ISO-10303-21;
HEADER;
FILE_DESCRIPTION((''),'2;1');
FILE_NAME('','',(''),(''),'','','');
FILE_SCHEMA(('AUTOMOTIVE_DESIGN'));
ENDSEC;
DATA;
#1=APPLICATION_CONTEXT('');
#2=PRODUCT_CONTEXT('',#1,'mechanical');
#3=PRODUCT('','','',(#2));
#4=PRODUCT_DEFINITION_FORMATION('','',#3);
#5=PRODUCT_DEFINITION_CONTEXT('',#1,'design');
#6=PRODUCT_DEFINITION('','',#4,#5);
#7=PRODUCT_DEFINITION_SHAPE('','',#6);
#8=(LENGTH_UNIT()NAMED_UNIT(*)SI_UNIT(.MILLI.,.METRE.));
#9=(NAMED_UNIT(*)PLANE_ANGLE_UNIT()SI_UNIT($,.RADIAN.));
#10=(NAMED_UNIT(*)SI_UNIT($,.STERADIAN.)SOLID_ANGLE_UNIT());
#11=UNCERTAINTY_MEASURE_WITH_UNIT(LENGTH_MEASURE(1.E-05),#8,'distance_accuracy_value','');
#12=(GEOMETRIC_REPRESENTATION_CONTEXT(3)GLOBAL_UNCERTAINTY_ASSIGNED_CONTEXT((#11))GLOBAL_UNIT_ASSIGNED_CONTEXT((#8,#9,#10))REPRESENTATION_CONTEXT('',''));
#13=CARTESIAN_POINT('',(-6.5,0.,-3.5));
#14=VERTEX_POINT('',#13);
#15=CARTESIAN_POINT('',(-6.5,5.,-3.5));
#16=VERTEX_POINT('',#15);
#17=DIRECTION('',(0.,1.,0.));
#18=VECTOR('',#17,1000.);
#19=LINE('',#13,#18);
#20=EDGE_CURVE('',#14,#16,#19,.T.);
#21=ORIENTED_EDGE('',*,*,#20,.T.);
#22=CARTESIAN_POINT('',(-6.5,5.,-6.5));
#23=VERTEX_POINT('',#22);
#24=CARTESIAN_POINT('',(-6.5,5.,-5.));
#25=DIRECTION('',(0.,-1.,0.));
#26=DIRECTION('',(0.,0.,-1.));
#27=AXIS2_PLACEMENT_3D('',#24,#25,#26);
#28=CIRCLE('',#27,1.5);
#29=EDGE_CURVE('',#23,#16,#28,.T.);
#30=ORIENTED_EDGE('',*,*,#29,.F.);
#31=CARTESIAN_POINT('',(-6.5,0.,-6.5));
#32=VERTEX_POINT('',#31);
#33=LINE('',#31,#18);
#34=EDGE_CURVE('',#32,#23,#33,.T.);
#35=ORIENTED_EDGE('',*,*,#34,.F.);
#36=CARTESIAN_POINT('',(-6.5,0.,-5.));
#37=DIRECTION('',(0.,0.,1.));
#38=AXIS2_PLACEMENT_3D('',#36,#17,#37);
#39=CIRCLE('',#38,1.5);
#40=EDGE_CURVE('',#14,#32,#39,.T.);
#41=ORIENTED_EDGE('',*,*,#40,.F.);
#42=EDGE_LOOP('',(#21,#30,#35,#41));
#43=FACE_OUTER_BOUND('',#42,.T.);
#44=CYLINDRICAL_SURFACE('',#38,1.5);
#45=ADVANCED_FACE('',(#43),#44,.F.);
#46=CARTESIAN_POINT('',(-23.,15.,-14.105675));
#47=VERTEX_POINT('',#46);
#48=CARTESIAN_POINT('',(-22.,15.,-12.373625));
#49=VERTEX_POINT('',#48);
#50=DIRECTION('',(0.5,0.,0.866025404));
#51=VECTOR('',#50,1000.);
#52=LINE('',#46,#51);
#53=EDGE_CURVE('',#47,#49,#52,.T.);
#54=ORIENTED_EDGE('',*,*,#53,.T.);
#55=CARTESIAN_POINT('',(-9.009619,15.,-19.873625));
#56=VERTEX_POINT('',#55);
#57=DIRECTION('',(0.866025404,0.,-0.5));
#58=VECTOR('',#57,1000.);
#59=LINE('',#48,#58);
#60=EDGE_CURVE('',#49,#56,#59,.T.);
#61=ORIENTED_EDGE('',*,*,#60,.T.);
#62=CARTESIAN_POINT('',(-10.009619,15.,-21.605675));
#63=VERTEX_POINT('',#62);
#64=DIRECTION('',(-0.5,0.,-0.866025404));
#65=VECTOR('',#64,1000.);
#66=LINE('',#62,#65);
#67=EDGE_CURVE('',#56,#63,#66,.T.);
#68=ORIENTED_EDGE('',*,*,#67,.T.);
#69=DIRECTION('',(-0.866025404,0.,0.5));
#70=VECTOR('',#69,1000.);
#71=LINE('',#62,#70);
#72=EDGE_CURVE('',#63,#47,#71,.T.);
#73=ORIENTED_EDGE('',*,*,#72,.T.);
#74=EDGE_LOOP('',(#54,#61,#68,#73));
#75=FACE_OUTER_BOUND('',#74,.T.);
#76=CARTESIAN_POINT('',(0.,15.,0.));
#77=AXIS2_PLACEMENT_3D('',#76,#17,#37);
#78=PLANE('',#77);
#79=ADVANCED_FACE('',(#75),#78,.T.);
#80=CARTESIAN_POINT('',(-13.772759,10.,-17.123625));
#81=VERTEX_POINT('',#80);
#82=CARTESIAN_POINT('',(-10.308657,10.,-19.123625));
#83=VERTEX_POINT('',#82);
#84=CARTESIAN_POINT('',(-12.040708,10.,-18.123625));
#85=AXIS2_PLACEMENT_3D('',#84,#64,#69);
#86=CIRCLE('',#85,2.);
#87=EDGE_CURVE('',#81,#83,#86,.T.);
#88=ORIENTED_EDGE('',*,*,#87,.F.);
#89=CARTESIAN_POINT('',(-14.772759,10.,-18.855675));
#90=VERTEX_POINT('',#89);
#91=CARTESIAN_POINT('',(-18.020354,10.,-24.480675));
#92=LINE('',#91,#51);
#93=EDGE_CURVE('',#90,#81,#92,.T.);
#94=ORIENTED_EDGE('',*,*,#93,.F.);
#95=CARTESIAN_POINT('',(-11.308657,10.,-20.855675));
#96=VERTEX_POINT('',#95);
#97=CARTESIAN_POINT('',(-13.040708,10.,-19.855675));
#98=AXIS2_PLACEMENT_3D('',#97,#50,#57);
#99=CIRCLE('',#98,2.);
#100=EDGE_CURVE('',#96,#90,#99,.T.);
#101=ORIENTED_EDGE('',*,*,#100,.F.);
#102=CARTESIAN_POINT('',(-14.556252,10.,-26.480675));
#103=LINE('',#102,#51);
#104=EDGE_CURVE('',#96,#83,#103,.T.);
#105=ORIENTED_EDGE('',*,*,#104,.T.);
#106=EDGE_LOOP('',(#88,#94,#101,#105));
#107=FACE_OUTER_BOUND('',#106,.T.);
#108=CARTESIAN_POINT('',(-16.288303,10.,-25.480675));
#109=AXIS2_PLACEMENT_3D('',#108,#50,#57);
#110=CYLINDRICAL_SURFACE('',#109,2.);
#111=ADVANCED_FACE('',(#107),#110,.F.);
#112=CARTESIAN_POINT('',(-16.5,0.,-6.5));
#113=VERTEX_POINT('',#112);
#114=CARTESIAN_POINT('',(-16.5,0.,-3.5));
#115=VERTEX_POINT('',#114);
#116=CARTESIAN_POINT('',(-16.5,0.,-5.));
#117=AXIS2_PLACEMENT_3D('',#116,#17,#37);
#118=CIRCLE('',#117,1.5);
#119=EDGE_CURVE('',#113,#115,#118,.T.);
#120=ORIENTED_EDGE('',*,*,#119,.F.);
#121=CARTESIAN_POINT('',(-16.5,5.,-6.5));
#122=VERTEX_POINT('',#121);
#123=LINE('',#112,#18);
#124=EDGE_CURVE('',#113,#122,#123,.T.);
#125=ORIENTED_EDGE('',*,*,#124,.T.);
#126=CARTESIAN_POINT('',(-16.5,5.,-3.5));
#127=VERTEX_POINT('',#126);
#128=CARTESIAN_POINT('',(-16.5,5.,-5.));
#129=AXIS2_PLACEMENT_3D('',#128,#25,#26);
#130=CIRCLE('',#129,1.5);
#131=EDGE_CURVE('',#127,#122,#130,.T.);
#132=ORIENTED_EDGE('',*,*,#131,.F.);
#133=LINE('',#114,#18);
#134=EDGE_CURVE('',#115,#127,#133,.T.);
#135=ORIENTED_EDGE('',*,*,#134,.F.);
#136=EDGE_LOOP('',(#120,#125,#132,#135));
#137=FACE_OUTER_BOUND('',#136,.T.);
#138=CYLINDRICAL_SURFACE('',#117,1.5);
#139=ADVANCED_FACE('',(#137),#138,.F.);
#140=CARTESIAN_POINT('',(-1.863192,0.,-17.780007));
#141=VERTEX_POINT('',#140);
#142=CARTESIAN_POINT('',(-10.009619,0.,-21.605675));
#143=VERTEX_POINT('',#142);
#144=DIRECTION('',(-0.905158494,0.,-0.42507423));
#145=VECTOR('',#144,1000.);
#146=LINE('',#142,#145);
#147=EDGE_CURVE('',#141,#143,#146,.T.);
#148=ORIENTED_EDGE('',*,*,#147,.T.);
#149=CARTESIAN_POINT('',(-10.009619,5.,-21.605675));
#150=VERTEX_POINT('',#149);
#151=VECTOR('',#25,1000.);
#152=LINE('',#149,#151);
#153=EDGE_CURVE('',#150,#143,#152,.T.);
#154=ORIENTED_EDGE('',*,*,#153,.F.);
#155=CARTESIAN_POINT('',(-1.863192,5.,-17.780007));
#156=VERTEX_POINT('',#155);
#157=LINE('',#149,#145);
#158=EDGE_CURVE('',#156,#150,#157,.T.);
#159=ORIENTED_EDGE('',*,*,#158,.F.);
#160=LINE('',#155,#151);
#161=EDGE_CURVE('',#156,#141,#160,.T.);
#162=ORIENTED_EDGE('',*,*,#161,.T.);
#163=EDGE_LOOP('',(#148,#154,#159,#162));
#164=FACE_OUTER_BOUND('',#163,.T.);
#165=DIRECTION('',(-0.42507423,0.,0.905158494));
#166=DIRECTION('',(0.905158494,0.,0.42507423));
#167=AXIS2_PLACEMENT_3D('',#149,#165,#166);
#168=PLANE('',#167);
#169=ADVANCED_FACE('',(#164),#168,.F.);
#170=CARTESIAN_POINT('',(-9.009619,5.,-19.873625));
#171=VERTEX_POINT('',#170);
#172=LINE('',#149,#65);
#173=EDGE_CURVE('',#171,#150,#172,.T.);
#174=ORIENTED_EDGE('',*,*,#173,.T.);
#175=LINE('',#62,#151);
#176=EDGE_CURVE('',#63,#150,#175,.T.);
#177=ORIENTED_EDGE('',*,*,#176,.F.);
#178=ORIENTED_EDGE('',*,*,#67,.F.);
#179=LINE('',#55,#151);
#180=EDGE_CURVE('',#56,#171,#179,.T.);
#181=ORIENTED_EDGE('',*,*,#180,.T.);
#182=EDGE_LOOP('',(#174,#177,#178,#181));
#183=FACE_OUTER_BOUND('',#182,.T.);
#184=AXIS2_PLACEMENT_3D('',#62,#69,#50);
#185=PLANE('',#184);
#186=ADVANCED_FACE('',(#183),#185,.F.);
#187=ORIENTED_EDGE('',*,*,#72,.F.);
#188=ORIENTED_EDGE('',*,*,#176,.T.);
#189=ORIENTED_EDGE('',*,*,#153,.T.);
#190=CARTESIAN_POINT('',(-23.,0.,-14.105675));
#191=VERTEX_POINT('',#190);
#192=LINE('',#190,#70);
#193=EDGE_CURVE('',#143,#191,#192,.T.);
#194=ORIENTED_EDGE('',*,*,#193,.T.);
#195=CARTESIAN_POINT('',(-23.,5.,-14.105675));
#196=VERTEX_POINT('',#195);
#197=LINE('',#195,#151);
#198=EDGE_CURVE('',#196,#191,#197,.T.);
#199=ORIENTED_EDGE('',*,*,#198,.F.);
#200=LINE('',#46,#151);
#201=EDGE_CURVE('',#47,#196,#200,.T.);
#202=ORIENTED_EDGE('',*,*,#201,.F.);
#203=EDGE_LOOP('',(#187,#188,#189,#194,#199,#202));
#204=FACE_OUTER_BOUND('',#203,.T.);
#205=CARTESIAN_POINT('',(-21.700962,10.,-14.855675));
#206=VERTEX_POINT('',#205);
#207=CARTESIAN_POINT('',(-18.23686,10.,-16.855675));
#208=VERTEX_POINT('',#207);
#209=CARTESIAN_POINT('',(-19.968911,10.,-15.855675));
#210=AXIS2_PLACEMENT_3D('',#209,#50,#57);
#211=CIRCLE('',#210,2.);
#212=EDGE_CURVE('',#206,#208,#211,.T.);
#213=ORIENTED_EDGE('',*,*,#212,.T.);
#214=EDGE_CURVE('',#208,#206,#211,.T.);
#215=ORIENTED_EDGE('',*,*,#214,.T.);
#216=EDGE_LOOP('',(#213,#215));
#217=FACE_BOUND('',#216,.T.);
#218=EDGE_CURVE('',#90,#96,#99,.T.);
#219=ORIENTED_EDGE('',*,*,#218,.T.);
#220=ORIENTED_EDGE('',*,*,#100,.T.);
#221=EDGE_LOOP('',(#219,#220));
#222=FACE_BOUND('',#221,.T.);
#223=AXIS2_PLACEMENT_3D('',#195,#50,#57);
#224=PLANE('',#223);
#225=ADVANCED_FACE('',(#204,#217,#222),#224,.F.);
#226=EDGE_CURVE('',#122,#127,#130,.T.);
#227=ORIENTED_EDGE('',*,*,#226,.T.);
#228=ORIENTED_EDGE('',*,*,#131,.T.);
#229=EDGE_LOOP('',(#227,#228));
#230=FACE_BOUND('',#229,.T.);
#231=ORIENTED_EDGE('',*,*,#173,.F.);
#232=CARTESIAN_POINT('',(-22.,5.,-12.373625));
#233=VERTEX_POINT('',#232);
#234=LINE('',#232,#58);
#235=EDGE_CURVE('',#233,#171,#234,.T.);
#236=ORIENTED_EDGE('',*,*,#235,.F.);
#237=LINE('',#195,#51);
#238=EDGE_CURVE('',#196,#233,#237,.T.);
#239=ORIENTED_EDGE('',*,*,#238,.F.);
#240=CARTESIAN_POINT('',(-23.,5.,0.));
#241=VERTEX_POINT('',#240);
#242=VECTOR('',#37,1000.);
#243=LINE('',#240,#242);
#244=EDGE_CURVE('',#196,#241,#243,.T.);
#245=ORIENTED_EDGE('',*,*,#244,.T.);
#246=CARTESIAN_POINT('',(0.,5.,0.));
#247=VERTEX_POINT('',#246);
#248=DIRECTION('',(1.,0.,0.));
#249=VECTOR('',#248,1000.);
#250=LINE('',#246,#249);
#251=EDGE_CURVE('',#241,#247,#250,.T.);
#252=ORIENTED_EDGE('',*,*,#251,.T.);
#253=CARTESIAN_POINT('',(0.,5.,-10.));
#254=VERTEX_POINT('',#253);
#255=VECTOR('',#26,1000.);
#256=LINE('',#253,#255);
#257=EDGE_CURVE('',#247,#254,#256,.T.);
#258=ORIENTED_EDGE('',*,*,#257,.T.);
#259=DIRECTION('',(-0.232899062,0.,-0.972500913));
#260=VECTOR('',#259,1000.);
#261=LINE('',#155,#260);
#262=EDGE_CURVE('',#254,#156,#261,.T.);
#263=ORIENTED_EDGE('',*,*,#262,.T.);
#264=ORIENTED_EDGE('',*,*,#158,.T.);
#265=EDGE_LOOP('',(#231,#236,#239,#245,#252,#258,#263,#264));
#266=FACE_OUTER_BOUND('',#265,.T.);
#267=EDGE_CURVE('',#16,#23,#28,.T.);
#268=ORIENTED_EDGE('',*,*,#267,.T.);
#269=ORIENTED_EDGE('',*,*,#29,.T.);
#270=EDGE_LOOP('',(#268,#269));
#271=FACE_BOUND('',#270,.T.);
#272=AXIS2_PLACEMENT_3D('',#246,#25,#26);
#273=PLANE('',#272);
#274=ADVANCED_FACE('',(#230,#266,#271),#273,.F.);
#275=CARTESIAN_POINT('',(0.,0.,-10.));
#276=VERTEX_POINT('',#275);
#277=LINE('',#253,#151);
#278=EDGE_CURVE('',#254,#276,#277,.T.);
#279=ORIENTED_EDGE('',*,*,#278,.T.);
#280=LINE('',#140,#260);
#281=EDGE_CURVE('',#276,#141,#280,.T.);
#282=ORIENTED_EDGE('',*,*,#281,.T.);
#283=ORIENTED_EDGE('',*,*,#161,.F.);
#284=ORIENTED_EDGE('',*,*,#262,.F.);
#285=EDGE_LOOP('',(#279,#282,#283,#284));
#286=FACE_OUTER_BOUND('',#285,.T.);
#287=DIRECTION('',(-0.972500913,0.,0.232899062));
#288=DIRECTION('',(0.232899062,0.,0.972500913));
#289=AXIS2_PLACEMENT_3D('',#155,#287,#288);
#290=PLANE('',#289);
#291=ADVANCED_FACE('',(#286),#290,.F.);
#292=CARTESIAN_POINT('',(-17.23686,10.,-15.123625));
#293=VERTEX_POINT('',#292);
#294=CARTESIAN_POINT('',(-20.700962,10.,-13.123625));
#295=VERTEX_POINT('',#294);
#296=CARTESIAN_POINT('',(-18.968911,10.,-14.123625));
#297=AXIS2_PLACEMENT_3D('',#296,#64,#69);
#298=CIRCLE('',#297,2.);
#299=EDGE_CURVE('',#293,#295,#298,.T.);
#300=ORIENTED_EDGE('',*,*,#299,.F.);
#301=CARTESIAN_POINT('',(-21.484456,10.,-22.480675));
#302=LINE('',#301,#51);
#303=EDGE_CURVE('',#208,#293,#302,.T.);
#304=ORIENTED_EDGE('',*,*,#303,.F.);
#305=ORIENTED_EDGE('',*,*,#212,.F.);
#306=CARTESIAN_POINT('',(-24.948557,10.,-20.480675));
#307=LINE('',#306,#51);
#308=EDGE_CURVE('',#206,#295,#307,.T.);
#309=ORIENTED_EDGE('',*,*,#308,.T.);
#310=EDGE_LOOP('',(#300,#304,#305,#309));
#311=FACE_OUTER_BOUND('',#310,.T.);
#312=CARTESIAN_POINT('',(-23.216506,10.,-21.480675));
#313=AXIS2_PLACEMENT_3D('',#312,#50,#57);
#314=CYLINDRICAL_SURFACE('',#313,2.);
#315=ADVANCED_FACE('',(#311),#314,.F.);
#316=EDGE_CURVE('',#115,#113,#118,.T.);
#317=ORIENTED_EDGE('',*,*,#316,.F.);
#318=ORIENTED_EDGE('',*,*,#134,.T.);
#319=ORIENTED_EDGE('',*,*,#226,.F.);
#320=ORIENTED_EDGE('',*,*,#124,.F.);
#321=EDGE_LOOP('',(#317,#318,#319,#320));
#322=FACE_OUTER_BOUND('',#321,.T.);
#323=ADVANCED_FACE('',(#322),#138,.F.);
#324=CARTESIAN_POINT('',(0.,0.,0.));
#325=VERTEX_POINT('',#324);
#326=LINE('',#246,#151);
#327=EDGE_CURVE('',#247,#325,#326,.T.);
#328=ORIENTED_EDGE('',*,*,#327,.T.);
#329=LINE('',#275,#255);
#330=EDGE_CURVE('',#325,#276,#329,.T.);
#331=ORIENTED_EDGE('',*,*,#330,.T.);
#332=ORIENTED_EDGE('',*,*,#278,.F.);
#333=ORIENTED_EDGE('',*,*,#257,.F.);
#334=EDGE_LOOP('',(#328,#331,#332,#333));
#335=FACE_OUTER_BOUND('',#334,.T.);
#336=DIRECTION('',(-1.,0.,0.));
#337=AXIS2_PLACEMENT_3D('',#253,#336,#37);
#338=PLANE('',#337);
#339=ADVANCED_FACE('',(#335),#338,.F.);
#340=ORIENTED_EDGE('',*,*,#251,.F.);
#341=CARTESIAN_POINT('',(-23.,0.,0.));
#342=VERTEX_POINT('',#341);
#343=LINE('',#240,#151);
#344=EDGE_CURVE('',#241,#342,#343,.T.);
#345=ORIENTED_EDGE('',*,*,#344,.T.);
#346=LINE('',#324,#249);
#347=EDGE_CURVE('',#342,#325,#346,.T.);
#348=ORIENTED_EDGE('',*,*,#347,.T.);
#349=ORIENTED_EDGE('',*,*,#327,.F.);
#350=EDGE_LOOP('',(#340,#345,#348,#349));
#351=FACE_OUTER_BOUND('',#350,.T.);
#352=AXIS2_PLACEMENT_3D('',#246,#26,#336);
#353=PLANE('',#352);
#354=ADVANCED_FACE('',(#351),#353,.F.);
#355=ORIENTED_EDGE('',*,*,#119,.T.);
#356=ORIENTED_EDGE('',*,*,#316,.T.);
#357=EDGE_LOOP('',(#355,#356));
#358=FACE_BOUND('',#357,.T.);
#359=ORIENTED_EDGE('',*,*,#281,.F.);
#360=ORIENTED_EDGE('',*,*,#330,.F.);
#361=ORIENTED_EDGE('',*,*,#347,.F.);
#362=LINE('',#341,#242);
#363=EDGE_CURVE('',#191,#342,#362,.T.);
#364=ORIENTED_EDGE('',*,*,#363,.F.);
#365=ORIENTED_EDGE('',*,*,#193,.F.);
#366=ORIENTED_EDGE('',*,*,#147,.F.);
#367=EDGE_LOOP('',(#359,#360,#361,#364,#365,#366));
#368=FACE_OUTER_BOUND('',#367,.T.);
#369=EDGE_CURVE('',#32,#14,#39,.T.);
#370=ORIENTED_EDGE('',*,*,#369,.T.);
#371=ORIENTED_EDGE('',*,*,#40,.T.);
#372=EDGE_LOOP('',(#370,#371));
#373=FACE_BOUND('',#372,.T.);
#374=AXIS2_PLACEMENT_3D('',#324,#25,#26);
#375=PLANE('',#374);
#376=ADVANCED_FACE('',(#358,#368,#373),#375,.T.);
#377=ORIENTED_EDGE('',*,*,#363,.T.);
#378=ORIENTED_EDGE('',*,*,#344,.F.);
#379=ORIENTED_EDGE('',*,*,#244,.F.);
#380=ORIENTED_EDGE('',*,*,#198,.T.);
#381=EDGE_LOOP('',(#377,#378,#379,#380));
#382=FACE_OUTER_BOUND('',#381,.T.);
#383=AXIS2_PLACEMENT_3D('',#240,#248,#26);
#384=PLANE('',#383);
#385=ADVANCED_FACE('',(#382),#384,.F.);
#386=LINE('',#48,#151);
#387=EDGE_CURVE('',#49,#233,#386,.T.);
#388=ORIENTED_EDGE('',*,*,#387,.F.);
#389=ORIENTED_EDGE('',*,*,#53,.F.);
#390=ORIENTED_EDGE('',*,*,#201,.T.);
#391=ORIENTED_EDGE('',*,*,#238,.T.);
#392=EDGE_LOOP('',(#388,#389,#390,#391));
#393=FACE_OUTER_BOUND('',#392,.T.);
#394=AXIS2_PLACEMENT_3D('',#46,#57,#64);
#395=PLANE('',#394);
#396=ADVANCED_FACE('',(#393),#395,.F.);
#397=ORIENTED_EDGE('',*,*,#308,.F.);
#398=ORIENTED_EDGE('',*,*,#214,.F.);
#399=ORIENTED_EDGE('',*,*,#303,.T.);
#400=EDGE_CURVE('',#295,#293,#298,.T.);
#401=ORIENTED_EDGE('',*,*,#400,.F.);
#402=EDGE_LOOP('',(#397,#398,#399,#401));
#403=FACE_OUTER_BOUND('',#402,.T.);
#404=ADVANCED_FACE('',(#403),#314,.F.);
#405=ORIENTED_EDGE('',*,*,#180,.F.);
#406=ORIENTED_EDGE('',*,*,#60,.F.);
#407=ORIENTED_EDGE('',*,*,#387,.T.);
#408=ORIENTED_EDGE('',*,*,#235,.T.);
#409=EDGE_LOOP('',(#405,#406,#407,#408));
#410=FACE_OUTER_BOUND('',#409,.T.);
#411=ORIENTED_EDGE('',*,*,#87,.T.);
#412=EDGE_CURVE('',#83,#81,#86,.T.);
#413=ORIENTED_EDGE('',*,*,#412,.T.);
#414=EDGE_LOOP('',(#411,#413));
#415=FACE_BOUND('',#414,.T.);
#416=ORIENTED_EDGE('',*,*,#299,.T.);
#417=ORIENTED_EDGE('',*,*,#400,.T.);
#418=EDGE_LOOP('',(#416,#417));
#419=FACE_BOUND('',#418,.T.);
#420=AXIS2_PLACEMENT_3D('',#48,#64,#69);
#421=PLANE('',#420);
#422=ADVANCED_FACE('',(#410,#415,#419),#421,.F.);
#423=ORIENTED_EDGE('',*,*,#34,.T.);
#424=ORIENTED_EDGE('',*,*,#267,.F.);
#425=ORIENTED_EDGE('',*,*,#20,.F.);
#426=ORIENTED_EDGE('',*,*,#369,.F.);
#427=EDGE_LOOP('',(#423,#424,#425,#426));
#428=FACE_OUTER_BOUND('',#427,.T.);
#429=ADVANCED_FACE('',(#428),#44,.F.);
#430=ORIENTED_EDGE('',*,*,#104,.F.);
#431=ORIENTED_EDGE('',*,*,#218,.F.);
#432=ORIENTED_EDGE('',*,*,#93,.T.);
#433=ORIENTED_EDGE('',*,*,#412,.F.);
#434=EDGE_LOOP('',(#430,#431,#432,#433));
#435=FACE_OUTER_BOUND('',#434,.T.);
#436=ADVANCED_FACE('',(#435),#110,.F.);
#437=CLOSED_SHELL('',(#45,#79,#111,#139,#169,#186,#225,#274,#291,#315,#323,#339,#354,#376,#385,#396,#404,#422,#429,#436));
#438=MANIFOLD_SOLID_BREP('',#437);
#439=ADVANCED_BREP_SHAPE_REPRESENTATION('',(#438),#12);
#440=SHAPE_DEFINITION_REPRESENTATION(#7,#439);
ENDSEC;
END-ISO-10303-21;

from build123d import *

# Parameters (mm, degrees)
BOSS_EXTRUDE1_DEPTH     = 5
BOSS_EXTRUDE2_DEPTH     = 10
CUT_EXTRUDE1_DEPTH      = 27.946503772
CUT_EXTRUDE1_DEPTH_BACK = 27.946503772
SKETCH3_R               = 2
CUT_EXTRUDE2_DEPTH      = 34.102948638
CUT_EXTRUDE2_DEPTH_BACK = 34.102948638
SKETCH4_R               = 1.5


with BuildPart() as part:
    # Sketch1 → Boss-Extrude1 (new body)
    with BuildSketch(Plane(origin=(0, 0, 0), x_dir=(1, 0, 0), z_dir=(0, 1, 0))):
        Polygon((0, 0), (-23, 0), (-23, 14.105675379), (-10.009618943, 21.605675379), (-1.863192499, 17.780007308), (0, 10), align=None)
    extrude(amount=BOSS_EXTRUDE1_DEPTH)

    # Sketch2 → Boss-Extrude2 (add)
    with BuildSketch(Plane(origin=(0, 5, 0), x_dir=(1, 0, 0), z_dir=(0, 1, 0))):
        Polygon((-22, 12.373624571), (-9.009618943, 19.873624571), (-10.009618943, 21.605675379), (-23, 14.105675379), align=None)
    extrude(amount=BOSS_EXTRUDE2_DEPTH)

    # Sketch3 → Cut-Extrude1 (cut, two sides: drawn at the far end of the back side and taken through both)
    with BuildSketch(Plane(origin=(-10.857936608, 0, -18.80649787), x_dir=(0.8660254037844384, 0, -0.5000000000000004), z_dir=(0.5000000000000004, 0, 0.8660254037844384)).offset(-CUT_EXTRUDE1_DEPTH_BACK)):
        with Locations((-9.365746598, 10)):
            Circle(SKETCH3_R)
        with Locations((-1.365746598, 10)):
            Circle(SKETCH3_R)
    extrude(amount=CUT_EXTRUDE1_DEPTH + CUT_EXTRUDE1_DEPTH_BACK, mode=Mode.SUBTRACT)

    # Sketch4 → Cut-Extrude2 (cut, two sides: drawn at the far end of the back side and taken through both)
    with BuildSketch(Plane(origin=(0, 5, 0), x_dir=(1, 0, 0), z_dir=(0, 1, 0)).offset(-CUT_EXTRUDE2_DEPTH_BACK)):
        with Locations(Location((-16.5, 5, 0), (0, 0, 270))):
            Circle(SKETCH4_R)
        with Locations(Location((-6.5, 5, 0), (0, 0, 270))):
            Circle(SKETCH4_R)
    extrude(amount=CUT_EXTRUDE2_DEPTH + CUT_EXTRUDE2_DEPTH_BACK, mode=Mode.SUBTRACT)


solid = part.part
